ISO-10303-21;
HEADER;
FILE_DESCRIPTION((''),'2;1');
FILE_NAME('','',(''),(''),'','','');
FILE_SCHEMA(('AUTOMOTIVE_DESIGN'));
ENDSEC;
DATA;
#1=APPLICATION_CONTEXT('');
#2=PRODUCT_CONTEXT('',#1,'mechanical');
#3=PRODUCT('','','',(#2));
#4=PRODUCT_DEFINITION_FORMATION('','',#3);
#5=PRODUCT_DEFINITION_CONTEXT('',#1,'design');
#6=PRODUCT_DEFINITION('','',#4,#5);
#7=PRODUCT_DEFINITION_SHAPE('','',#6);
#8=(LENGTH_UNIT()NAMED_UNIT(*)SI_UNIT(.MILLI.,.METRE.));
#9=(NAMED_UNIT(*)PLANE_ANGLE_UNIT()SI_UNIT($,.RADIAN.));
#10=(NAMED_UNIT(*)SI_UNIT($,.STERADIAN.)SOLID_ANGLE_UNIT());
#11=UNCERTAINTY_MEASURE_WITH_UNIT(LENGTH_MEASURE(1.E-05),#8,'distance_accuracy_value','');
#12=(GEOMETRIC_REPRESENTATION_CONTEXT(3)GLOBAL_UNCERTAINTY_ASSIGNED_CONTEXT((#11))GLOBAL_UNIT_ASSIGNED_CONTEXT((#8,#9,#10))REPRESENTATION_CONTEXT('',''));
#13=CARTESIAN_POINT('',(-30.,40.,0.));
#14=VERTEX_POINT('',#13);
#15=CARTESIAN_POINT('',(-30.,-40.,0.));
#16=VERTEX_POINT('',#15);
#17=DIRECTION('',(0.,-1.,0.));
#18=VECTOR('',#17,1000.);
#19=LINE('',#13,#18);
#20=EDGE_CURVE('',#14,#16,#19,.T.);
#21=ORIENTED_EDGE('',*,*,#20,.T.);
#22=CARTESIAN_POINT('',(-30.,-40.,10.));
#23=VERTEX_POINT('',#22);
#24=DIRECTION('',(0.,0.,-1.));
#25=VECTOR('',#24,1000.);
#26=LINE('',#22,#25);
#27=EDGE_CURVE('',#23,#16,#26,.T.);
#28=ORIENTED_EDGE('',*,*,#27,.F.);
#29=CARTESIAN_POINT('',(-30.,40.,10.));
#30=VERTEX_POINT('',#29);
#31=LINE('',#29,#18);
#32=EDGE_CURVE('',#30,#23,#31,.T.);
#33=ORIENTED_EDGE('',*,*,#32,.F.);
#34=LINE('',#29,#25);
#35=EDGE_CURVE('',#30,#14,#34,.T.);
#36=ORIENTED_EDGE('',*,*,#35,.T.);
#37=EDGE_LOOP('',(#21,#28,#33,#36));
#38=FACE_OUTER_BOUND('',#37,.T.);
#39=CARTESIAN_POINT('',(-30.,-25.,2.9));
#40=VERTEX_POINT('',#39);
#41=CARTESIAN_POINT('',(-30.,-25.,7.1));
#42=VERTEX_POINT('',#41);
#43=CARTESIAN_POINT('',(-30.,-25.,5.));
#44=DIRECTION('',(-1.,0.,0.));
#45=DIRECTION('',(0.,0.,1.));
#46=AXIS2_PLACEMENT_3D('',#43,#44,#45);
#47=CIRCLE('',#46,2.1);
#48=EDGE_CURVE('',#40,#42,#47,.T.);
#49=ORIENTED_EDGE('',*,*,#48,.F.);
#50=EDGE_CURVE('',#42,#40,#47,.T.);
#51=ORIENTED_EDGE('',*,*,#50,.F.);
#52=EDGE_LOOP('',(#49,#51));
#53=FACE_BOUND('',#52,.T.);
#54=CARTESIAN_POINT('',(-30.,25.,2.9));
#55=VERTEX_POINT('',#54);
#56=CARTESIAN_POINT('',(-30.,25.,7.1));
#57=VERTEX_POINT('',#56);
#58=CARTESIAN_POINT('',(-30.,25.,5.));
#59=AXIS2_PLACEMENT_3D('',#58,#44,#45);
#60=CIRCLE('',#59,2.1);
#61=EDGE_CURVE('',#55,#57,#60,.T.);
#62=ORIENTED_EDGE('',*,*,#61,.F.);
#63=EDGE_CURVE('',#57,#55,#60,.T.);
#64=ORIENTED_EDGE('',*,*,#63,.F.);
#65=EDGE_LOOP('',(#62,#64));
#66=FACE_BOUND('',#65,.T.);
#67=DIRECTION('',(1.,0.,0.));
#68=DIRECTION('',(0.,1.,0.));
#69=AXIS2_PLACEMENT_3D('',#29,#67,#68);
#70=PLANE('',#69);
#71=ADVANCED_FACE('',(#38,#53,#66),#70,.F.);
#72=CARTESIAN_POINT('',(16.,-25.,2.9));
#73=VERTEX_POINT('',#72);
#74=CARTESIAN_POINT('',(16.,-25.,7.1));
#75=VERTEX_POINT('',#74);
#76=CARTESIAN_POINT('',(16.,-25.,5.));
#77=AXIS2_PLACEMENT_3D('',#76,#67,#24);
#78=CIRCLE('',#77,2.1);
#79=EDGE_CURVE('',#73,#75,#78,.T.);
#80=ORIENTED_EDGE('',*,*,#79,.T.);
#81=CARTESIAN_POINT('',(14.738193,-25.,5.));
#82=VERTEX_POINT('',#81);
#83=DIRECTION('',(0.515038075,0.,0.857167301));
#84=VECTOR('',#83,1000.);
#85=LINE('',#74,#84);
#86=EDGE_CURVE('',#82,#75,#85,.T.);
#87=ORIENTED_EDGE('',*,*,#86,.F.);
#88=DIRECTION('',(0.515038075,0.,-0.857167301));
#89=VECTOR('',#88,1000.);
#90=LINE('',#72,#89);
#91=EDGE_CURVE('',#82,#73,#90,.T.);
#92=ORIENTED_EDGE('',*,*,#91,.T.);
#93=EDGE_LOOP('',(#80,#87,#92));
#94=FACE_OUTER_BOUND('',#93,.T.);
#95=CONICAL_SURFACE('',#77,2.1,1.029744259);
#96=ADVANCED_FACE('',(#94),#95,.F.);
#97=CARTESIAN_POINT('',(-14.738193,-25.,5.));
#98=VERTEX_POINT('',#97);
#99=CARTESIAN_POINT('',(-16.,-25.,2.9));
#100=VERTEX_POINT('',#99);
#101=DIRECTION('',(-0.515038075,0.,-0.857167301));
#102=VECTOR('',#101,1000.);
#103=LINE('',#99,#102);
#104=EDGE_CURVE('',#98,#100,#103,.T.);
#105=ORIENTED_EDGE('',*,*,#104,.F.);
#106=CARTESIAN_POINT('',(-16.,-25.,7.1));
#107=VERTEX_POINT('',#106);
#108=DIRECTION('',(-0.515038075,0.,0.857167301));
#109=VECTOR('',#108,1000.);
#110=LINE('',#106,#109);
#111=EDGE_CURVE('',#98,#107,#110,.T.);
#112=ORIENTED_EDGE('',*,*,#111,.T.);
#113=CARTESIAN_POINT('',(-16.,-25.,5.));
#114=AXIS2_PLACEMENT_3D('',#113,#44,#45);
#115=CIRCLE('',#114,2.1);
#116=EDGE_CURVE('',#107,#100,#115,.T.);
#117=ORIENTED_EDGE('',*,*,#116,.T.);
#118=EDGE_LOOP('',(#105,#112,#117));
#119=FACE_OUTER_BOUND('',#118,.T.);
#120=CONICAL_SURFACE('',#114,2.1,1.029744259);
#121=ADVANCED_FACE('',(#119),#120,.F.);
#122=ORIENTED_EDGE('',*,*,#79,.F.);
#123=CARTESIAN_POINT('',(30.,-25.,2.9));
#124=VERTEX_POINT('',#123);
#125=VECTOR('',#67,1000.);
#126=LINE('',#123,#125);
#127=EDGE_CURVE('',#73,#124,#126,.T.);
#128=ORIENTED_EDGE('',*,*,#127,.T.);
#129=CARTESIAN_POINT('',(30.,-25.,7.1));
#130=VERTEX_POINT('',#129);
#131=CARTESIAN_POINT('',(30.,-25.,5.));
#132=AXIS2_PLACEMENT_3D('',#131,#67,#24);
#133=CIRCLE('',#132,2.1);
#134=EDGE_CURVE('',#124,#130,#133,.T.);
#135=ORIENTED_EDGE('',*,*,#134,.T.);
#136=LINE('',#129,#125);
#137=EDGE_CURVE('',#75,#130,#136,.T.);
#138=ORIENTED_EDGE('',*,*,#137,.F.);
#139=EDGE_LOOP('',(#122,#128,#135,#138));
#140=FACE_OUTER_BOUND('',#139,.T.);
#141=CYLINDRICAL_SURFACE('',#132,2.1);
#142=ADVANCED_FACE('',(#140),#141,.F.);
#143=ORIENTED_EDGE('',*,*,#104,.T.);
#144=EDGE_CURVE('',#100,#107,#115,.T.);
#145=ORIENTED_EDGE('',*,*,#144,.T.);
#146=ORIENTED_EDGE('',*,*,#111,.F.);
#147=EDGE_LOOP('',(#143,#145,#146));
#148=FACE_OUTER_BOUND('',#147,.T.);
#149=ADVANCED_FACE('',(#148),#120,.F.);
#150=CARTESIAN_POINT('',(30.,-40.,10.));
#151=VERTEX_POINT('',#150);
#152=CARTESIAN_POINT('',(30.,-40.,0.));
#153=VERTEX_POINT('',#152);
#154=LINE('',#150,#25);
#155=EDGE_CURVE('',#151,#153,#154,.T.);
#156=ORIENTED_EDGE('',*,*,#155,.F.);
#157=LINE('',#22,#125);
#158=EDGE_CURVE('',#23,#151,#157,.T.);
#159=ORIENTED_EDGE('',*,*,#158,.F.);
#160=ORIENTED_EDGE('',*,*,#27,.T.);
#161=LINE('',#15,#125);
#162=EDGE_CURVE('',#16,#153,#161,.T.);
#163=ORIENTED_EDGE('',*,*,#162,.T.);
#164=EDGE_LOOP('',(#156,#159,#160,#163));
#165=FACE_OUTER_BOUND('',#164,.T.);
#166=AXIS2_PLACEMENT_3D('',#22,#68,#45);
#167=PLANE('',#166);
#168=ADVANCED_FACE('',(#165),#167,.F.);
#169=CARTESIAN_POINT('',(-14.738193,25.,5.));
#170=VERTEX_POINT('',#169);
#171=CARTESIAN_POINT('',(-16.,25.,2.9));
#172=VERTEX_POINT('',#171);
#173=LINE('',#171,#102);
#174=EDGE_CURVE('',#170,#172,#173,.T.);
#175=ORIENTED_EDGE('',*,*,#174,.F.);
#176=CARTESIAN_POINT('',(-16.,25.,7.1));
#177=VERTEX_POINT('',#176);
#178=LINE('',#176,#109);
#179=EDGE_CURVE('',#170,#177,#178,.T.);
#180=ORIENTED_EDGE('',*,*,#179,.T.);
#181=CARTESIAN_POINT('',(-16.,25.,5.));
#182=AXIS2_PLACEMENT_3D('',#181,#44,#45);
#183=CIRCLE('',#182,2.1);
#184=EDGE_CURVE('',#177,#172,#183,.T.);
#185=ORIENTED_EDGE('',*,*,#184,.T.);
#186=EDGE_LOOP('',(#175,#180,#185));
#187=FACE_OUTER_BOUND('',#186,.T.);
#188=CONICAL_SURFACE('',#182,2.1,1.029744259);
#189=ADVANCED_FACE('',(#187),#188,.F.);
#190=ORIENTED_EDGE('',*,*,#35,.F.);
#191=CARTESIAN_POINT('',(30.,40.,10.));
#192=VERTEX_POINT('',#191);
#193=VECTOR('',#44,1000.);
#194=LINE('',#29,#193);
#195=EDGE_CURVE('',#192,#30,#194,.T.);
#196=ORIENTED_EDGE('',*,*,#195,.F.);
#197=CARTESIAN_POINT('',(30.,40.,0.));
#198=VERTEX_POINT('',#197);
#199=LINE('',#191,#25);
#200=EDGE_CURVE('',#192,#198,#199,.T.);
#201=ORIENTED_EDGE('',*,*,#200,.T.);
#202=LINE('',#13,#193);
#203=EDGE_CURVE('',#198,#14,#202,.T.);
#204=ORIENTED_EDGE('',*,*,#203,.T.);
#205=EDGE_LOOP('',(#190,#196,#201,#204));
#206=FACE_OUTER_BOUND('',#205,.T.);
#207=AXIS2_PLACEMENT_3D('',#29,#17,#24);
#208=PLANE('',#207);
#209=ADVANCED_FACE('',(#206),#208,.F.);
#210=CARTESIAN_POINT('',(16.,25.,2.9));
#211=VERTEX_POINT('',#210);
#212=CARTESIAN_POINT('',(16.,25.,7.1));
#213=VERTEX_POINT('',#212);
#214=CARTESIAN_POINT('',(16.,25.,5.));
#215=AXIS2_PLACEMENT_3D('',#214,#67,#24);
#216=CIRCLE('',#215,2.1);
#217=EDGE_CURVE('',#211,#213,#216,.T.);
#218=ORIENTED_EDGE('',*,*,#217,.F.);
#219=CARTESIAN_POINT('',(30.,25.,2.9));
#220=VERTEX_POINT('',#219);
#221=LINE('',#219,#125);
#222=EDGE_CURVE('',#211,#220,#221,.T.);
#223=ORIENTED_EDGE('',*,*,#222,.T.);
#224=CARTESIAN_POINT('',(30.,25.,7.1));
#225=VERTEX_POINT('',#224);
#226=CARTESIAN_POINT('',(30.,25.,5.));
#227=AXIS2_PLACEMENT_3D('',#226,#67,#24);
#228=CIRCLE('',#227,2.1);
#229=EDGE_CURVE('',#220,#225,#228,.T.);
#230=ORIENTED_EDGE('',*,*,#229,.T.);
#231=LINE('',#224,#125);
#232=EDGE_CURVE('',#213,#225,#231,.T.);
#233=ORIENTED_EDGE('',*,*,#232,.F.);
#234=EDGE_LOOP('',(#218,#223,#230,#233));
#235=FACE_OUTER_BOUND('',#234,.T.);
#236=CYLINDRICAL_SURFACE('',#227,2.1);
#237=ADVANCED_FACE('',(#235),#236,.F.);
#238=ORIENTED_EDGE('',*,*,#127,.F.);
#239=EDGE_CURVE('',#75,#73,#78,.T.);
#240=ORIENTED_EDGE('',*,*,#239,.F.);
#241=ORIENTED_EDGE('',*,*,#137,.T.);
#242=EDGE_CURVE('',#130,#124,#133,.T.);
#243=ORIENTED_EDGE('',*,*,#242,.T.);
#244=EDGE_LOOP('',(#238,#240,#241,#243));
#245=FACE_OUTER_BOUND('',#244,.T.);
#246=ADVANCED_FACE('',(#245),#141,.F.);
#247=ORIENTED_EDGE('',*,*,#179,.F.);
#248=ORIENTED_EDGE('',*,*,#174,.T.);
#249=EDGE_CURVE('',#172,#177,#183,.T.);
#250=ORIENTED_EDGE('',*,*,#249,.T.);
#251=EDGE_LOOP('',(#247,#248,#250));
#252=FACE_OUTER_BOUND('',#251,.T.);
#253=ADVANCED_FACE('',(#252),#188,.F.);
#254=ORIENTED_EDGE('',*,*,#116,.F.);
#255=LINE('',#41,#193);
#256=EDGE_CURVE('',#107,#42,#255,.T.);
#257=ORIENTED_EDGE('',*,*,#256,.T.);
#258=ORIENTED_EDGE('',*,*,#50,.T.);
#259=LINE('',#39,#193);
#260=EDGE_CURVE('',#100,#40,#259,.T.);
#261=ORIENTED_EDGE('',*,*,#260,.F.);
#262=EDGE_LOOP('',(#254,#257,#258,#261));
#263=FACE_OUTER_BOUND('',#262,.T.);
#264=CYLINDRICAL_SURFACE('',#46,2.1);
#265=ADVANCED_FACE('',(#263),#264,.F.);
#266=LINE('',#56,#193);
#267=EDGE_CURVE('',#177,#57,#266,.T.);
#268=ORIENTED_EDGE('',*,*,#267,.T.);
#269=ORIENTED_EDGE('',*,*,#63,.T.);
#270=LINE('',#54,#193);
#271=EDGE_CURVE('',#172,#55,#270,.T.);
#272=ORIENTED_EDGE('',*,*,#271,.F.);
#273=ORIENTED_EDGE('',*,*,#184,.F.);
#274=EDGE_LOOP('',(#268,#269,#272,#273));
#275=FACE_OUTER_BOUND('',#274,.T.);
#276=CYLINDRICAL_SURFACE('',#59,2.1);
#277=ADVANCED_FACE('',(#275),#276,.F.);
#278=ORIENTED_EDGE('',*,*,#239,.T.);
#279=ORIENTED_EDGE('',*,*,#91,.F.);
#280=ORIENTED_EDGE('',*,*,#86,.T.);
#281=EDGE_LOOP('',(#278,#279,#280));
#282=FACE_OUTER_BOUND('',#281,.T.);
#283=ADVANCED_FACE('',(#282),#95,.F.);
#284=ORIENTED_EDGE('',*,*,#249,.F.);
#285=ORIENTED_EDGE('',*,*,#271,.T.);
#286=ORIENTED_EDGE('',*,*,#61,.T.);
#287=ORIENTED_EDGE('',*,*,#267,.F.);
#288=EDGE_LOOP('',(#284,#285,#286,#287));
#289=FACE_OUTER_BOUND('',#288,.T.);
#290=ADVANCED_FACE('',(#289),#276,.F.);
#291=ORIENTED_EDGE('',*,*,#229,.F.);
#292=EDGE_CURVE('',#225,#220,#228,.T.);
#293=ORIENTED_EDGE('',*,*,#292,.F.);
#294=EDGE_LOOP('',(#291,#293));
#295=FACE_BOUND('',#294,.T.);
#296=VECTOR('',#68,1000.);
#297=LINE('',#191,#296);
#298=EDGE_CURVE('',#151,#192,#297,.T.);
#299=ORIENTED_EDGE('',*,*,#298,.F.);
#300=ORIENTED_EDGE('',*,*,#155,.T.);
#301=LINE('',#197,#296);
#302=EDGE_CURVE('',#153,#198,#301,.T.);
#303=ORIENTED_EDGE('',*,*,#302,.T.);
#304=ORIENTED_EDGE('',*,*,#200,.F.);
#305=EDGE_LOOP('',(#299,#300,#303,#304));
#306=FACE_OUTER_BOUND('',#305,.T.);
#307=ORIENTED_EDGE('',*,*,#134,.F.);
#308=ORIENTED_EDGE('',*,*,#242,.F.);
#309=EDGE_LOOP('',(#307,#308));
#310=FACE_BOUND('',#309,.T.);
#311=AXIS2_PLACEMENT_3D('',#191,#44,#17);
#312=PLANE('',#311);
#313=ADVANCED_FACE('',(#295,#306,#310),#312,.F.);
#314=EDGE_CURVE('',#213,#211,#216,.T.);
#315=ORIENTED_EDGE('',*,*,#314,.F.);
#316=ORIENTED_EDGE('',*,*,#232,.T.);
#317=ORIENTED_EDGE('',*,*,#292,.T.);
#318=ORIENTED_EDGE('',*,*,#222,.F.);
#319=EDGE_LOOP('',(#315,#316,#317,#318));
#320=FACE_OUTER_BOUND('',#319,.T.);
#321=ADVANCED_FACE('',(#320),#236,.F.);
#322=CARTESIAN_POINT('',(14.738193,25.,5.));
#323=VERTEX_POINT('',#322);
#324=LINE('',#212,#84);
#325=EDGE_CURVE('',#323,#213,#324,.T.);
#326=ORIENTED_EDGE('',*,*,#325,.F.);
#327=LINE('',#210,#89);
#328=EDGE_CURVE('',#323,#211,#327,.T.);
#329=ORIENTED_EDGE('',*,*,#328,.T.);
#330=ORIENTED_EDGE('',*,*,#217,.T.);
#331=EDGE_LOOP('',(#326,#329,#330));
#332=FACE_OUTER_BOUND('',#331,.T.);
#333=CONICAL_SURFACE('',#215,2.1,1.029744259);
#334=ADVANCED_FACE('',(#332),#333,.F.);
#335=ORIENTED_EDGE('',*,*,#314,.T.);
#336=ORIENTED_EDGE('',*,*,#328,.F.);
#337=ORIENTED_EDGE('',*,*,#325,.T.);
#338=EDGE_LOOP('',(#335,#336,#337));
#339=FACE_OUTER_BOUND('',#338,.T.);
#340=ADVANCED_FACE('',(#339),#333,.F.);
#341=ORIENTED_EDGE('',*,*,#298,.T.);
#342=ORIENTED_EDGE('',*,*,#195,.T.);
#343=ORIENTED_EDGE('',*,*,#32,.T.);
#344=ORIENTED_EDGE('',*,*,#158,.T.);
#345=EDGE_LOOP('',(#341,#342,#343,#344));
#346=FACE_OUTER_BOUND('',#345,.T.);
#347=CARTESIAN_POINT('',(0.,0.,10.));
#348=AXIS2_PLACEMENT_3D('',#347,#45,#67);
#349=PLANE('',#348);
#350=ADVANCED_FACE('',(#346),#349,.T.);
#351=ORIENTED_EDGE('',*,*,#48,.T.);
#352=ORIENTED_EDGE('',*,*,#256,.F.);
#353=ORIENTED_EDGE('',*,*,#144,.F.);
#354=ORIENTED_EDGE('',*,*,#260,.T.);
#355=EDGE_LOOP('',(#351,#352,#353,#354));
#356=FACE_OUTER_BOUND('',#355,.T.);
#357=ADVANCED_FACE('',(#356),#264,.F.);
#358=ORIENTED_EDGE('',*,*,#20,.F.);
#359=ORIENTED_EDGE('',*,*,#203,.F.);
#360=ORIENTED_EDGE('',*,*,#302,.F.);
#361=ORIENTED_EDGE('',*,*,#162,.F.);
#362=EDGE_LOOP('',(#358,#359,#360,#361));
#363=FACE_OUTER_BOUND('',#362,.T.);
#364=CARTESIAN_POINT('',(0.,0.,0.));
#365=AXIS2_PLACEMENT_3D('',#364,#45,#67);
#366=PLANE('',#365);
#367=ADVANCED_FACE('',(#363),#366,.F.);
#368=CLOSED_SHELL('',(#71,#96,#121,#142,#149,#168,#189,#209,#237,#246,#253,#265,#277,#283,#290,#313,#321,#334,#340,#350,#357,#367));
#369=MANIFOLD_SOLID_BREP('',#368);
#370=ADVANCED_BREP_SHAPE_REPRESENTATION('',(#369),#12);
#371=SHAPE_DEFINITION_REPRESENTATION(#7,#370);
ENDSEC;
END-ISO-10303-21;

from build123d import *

# Parameters (mm, degrees)
SKETCH_1_W             = 60
SKETCH_1_H             = 80
EXTRUDE_1_DEPTH        = 10
HOLE_WIZARD_M5_1_D     = 4.2
HOLE_WIZARD_M5_1_DEPTH = 14
HOLE_WIZARD_M5_1_TIP   = 1.2618073
HOLE_WIZARD_M5_2_D     = 4.2
HOLE_WIZARD_M5_2_DEPTH = 14
HOLE_WIZARD_M5_2_TIP   = 1.2618073


with BuildPart() as part:
    # 草图1 → 凸台-拉伸1 (new body)
    with BuildSketch(Plane.XY):
        Rectangle(SKETCH_1_W, SKETCH_1_H)
    extrude(amount=EXTRUDE_1_DEPTH)

    # M5 螺纹孔1
    with Locations(Plane(origin=(30, 0, 0), x_dir=(0, 0, -1), z_dir=(1, 0, 0))):
        with Locations((-5, -25), (-5, 25)):
            Hole(HOLE_WIZARD_M5_1_D / 2, depth=HOLE_WIZARD_M5_1_DEPTH)
            with Locations((0, 0, -(HOLE_WIZARD_M5_1_DEPTH + HOLE_WIZARD_M5_1_TIP / 2))):  # 118° drill point
                Cone(0, HOLE_WIZARD_M5_1_D / 2, HOLE_WIZARD_M5_1_TIP, mode=Mode.SUBTRACT)

    # M5 螺纹孔2
    with Locations(Plane.ZY.offset(30)):
        with Locations((5, 25), (5, -25)):
            Hole(HOLE_WIZARD_M5_2_D / 2, depth=HOLE_WIZARD_M5_2_DEPTH)
            with Locations((0, 0, -(HOLE_WIZARD_M5_2_DEPTH + HOLE_WIZARD_M5_2_TIP / 2))):  # 118° drill point
                Cone(0, HOLE_WIZARD_M5_2_D / 2, HOLE_WIZARD_M5_2_TIP, mode=Mode.SUBTRACT)


solid = part.part
